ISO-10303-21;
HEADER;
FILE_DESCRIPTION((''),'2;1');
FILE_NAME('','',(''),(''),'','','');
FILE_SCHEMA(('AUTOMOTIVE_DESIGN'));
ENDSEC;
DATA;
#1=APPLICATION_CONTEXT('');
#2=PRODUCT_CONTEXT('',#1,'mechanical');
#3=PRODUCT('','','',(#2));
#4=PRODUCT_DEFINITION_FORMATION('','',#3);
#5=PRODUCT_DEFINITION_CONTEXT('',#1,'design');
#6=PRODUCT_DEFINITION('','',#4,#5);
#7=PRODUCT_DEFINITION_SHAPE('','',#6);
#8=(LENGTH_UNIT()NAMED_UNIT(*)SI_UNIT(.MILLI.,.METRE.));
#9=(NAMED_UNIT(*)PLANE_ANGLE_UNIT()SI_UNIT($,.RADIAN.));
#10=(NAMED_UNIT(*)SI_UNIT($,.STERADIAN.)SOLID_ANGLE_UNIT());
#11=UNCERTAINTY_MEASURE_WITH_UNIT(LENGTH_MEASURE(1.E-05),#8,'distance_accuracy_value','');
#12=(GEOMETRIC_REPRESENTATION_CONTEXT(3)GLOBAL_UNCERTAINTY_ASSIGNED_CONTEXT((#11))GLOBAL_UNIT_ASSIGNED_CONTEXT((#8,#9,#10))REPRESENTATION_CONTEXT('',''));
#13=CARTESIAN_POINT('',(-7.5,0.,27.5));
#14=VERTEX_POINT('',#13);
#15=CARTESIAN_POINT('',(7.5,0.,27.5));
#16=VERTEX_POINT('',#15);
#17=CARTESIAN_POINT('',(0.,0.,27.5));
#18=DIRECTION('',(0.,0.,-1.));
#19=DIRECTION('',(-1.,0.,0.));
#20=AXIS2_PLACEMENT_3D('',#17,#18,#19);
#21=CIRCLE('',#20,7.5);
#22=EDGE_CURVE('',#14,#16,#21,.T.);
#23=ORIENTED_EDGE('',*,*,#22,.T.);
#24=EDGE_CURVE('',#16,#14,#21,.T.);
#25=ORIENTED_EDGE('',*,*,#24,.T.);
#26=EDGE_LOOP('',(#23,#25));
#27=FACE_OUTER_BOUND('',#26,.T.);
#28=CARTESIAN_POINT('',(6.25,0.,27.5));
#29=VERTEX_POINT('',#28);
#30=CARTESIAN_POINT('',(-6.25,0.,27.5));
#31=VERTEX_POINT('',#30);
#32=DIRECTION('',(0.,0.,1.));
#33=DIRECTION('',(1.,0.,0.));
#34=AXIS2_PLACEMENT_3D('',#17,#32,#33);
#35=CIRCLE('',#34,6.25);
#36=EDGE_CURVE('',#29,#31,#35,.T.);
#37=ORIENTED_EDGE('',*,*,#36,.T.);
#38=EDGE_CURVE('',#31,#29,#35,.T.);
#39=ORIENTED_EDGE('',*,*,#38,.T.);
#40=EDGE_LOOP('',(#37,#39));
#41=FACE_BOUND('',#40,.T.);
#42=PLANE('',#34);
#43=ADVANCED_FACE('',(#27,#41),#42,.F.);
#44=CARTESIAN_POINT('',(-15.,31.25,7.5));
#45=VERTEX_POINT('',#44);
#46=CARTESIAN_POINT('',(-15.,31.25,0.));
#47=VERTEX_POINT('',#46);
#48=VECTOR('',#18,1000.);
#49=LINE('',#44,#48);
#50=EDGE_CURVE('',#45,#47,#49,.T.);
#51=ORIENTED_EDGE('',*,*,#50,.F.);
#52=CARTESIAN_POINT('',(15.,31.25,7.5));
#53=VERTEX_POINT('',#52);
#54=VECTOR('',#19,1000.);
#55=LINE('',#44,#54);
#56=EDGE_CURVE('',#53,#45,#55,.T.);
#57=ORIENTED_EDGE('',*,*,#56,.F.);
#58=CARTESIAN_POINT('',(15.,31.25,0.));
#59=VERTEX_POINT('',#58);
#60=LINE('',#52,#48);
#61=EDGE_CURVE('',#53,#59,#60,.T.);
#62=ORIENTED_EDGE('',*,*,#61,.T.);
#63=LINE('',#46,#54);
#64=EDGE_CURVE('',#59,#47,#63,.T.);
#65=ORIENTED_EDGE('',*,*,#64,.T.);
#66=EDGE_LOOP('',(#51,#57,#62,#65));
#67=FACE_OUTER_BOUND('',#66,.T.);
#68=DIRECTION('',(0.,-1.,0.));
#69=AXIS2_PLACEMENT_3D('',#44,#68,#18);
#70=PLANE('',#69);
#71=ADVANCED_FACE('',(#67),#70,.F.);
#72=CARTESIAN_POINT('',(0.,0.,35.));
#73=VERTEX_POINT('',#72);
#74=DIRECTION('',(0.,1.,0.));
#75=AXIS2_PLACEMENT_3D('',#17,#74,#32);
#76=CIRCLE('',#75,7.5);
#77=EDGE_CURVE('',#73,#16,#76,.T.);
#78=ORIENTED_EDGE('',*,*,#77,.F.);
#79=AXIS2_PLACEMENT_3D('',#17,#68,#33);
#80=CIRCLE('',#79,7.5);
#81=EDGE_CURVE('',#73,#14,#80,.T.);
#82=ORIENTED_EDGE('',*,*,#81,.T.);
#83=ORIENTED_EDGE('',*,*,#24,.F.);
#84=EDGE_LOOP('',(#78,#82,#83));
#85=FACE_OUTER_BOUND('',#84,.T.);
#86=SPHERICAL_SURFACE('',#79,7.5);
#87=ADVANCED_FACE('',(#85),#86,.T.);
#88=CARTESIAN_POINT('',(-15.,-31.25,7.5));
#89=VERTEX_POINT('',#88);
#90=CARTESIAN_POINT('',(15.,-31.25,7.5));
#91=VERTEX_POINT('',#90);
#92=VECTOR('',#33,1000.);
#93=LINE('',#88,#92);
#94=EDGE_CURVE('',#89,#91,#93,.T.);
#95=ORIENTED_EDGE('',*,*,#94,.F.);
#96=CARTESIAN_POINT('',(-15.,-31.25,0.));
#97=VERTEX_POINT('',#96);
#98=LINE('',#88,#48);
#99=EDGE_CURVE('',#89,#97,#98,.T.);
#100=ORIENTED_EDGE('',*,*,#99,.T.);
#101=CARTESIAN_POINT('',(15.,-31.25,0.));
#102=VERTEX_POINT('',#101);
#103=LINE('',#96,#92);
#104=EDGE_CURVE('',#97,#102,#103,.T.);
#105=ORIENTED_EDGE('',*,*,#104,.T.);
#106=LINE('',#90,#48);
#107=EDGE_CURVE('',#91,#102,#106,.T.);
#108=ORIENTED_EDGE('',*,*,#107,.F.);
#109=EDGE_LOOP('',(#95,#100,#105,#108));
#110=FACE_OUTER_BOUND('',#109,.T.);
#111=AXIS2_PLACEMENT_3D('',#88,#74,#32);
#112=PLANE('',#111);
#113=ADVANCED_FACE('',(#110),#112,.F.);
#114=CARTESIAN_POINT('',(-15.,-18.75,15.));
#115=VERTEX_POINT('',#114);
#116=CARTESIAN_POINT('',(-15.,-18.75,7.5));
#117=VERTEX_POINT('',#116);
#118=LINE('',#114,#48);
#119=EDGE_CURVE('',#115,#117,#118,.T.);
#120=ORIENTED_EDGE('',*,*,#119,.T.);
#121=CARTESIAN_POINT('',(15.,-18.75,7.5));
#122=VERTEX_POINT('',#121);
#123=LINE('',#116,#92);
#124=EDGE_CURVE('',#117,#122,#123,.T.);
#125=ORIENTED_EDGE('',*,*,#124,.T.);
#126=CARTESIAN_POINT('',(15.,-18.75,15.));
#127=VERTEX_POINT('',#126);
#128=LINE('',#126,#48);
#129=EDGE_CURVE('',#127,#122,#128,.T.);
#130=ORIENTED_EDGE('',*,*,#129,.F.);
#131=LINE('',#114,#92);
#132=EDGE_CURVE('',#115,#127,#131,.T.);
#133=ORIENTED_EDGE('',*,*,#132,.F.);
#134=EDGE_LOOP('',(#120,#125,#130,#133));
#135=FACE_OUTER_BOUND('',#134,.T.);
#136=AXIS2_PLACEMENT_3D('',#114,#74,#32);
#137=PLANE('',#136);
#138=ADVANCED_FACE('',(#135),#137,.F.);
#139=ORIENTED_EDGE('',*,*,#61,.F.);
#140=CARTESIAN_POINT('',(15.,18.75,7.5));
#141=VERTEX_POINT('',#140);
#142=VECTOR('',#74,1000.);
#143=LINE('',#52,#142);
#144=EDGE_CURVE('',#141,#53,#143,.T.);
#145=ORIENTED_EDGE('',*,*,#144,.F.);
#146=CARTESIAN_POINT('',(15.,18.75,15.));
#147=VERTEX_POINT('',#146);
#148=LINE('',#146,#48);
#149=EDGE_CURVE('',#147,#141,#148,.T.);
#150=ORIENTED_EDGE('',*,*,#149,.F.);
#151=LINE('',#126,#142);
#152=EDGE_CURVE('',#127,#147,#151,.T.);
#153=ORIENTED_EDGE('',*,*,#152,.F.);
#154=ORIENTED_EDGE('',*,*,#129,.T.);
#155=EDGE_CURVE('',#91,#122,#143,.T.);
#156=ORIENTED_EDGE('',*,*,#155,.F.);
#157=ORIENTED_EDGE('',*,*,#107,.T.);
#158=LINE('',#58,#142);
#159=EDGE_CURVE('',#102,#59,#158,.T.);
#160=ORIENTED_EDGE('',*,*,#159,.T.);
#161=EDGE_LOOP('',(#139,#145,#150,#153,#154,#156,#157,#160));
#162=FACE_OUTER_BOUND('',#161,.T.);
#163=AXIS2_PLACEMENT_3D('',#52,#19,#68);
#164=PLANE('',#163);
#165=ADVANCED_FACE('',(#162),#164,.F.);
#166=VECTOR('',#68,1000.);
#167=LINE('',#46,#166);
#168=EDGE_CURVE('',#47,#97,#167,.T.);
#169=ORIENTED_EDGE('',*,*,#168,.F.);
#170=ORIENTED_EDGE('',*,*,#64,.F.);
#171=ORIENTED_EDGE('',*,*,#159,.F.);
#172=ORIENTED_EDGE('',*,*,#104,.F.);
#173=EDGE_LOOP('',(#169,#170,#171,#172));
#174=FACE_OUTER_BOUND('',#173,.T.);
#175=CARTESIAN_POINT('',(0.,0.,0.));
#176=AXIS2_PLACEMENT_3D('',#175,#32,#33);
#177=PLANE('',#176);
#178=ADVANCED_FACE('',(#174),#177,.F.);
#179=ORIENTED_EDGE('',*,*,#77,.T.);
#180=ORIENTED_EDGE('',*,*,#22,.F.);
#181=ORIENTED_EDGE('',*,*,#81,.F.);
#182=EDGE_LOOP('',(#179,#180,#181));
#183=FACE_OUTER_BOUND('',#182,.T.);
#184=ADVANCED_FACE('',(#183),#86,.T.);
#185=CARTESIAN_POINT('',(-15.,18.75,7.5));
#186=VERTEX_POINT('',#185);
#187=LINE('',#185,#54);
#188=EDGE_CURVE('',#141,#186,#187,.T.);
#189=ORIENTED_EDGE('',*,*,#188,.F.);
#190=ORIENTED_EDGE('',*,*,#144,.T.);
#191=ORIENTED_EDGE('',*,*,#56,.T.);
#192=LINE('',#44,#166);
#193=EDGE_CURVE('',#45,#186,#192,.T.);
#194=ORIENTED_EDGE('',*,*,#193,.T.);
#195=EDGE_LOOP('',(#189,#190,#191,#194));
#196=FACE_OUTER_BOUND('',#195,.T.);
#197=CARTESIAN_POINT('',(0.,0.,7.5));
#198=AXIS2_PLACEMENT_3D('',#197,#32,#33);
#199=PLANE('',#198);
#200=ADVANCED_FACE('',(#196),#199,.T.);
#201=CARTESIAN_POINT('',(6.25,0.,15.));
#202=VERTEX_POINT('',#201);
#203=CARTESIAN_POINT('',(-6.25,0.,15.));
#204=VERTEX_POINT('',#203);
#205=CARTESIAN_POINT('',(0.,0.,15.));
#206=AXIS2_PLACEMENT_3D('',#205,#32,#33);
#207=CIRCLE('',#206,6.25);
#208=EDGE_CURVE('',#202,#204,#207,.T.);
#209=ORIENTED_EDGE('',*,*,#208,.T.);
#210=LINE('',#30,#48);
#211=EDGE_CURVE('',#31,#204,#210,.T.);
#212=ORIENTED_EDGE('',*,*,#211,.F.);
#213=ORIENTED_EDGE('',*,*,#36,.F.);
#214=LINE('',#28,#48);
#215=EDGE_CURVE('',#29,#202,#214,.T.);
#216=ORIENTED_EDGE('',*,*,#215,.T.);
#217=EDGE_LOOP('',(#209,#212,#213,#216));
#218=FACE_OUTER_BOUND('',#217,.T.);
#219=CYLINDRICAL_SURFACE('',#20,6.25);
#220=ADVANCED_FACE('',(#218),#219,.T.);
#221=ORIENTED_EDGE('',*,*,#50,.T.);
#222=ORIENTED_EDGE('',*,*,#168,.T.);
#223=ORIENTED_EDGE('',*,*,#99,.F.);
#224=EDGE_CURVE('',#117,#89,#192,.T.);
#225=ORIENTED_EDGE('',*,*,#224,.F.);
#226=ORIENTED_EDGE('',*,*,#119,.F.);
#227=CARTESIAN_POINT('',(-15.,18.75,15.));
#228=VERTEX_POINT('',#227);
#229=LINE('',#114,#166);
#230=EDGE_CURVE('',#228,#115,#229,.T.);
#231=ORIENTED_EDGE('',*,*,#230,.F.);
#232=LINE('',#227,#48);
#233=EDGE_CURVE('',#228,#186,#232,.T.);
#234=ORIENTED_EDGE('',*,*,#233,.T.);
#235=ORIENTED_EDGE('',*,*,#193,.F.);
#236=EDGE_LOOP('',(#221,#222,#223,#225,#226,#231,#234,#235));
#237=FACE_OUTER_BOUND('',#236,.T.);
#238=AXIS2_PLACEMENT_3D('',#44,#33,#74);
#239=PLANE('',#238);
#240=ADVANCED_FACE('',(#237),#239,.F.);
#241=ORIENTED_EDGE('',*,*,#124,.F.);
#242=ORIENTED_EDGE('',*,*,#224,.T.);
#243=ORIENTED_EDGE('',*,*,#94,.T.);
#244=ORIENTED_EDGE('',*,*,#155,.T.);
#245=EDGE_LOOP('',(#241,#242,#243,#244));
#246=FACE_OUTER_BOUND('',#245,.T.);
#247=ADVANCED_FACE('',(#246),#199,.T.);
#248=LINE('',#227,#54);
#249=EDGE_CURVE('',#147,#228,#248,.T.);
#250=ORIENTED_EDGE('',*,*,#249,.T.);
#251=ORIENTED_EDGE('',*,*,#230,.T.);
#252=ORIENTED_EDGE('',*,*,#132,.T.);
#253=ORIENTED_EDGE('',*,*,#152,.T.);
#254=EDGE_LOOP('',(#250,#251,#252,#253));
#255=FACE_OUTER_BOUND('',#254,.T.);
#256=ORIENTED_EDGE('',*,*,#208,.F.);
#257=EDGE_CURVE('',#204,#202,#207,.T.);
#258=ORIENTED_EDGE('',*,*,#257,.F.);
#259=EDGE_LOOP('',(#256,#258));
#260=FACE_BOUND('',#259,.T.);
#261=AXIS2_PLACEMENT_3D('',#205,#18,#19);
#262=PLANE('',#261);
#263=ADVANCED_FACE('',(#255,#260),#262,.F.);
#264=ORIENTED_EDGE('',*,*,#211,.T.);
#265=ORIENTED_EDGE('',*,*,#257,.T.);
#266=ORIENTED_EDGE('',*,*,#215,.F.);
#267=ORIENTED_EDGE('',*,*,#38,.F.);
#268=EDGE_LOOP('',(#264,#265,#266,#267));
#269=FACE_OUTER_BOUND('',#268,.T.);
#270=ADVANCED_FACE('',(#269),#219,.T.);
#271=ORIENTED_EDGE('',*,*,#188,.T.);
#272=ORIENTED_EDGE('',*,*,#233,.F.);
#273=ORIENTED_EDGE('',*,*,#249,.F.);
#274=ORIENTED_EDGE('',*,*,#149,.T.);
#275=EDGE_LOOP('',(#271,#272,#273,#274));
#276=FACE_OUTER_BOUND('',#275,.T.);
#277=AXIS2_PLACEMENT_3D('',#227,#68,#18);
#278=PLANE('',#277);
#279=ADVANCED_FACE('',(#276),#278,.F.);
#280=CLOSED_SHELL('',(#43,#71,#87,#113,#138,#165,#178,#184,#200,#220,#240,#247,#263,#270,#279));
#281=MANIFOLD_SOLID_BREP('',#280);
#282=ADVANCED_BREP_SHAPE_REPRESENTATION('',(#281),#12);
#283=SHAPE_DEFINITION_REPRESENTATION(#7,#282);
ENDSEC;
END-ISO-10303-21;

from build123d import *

# Parameters (mm, degrees)
SKETCH1_W           = 12
SKETCH1_H           = 25
BOSS_EXTRUDE1_DEPTH = 3
SKETCH2_W           = 12
SKETCH2_H           = 15
BOSS_EXTRUDE2_DEPTH = 3
SKETCH3_R           = 2.5
BOSS_EXTRUDE3_DEPTH = 5
SCALE1_SCALE        = 2.5


with BuildPart() as part:
    # Sketch1 → Boss-Extrude1 (new body)
    with BuildSketch(Plane.XY):
        Rectangle(SKETCH1_W, SKETCH1_H)
    extrude(amount=BOSS_EXTRUDE1_DEPTH)

    # Sketch2 → Boss-Extrude2 (add)
    with BuildSketch(Plane.XY.offset(3)):
        Rectangle(SKETCH2_W, SKETCH2_H)
    extrude(amount=BOSS_EXTRUDE2_DEPTH)

    # Sketch3 → Boss-Extrude3 (add)
    with BuildSketch(Plane.XY.offset(6)):
        Circle(SKETCH3_R)
    extrude(amount=BOSS_EXTRUDE3_DEPTH)

    # Sketch4 → Revolve1 (revolve)
    with BuildSketch(Plane(origin=(0, 0, 0), x_dir=(1, 0, 0), z_dir=(0, 1, 0))):
        with BuildLine():
            Line((0, -11), (3, -11))
            ThreePointArc((3, -11), (2.121320344, -13.121320344), (0, -14))
            Line((0, -14), (0, -11))
        make_face()
    revolve(axis=Axis((0, 0, 11), (0, 0, 1)))


with BuildPart() as part_1:
    # Scale1: scaled about (0, 0, 0)
    add(part.part.scale(SCALE1_SCALE))


solid = part_1.part
